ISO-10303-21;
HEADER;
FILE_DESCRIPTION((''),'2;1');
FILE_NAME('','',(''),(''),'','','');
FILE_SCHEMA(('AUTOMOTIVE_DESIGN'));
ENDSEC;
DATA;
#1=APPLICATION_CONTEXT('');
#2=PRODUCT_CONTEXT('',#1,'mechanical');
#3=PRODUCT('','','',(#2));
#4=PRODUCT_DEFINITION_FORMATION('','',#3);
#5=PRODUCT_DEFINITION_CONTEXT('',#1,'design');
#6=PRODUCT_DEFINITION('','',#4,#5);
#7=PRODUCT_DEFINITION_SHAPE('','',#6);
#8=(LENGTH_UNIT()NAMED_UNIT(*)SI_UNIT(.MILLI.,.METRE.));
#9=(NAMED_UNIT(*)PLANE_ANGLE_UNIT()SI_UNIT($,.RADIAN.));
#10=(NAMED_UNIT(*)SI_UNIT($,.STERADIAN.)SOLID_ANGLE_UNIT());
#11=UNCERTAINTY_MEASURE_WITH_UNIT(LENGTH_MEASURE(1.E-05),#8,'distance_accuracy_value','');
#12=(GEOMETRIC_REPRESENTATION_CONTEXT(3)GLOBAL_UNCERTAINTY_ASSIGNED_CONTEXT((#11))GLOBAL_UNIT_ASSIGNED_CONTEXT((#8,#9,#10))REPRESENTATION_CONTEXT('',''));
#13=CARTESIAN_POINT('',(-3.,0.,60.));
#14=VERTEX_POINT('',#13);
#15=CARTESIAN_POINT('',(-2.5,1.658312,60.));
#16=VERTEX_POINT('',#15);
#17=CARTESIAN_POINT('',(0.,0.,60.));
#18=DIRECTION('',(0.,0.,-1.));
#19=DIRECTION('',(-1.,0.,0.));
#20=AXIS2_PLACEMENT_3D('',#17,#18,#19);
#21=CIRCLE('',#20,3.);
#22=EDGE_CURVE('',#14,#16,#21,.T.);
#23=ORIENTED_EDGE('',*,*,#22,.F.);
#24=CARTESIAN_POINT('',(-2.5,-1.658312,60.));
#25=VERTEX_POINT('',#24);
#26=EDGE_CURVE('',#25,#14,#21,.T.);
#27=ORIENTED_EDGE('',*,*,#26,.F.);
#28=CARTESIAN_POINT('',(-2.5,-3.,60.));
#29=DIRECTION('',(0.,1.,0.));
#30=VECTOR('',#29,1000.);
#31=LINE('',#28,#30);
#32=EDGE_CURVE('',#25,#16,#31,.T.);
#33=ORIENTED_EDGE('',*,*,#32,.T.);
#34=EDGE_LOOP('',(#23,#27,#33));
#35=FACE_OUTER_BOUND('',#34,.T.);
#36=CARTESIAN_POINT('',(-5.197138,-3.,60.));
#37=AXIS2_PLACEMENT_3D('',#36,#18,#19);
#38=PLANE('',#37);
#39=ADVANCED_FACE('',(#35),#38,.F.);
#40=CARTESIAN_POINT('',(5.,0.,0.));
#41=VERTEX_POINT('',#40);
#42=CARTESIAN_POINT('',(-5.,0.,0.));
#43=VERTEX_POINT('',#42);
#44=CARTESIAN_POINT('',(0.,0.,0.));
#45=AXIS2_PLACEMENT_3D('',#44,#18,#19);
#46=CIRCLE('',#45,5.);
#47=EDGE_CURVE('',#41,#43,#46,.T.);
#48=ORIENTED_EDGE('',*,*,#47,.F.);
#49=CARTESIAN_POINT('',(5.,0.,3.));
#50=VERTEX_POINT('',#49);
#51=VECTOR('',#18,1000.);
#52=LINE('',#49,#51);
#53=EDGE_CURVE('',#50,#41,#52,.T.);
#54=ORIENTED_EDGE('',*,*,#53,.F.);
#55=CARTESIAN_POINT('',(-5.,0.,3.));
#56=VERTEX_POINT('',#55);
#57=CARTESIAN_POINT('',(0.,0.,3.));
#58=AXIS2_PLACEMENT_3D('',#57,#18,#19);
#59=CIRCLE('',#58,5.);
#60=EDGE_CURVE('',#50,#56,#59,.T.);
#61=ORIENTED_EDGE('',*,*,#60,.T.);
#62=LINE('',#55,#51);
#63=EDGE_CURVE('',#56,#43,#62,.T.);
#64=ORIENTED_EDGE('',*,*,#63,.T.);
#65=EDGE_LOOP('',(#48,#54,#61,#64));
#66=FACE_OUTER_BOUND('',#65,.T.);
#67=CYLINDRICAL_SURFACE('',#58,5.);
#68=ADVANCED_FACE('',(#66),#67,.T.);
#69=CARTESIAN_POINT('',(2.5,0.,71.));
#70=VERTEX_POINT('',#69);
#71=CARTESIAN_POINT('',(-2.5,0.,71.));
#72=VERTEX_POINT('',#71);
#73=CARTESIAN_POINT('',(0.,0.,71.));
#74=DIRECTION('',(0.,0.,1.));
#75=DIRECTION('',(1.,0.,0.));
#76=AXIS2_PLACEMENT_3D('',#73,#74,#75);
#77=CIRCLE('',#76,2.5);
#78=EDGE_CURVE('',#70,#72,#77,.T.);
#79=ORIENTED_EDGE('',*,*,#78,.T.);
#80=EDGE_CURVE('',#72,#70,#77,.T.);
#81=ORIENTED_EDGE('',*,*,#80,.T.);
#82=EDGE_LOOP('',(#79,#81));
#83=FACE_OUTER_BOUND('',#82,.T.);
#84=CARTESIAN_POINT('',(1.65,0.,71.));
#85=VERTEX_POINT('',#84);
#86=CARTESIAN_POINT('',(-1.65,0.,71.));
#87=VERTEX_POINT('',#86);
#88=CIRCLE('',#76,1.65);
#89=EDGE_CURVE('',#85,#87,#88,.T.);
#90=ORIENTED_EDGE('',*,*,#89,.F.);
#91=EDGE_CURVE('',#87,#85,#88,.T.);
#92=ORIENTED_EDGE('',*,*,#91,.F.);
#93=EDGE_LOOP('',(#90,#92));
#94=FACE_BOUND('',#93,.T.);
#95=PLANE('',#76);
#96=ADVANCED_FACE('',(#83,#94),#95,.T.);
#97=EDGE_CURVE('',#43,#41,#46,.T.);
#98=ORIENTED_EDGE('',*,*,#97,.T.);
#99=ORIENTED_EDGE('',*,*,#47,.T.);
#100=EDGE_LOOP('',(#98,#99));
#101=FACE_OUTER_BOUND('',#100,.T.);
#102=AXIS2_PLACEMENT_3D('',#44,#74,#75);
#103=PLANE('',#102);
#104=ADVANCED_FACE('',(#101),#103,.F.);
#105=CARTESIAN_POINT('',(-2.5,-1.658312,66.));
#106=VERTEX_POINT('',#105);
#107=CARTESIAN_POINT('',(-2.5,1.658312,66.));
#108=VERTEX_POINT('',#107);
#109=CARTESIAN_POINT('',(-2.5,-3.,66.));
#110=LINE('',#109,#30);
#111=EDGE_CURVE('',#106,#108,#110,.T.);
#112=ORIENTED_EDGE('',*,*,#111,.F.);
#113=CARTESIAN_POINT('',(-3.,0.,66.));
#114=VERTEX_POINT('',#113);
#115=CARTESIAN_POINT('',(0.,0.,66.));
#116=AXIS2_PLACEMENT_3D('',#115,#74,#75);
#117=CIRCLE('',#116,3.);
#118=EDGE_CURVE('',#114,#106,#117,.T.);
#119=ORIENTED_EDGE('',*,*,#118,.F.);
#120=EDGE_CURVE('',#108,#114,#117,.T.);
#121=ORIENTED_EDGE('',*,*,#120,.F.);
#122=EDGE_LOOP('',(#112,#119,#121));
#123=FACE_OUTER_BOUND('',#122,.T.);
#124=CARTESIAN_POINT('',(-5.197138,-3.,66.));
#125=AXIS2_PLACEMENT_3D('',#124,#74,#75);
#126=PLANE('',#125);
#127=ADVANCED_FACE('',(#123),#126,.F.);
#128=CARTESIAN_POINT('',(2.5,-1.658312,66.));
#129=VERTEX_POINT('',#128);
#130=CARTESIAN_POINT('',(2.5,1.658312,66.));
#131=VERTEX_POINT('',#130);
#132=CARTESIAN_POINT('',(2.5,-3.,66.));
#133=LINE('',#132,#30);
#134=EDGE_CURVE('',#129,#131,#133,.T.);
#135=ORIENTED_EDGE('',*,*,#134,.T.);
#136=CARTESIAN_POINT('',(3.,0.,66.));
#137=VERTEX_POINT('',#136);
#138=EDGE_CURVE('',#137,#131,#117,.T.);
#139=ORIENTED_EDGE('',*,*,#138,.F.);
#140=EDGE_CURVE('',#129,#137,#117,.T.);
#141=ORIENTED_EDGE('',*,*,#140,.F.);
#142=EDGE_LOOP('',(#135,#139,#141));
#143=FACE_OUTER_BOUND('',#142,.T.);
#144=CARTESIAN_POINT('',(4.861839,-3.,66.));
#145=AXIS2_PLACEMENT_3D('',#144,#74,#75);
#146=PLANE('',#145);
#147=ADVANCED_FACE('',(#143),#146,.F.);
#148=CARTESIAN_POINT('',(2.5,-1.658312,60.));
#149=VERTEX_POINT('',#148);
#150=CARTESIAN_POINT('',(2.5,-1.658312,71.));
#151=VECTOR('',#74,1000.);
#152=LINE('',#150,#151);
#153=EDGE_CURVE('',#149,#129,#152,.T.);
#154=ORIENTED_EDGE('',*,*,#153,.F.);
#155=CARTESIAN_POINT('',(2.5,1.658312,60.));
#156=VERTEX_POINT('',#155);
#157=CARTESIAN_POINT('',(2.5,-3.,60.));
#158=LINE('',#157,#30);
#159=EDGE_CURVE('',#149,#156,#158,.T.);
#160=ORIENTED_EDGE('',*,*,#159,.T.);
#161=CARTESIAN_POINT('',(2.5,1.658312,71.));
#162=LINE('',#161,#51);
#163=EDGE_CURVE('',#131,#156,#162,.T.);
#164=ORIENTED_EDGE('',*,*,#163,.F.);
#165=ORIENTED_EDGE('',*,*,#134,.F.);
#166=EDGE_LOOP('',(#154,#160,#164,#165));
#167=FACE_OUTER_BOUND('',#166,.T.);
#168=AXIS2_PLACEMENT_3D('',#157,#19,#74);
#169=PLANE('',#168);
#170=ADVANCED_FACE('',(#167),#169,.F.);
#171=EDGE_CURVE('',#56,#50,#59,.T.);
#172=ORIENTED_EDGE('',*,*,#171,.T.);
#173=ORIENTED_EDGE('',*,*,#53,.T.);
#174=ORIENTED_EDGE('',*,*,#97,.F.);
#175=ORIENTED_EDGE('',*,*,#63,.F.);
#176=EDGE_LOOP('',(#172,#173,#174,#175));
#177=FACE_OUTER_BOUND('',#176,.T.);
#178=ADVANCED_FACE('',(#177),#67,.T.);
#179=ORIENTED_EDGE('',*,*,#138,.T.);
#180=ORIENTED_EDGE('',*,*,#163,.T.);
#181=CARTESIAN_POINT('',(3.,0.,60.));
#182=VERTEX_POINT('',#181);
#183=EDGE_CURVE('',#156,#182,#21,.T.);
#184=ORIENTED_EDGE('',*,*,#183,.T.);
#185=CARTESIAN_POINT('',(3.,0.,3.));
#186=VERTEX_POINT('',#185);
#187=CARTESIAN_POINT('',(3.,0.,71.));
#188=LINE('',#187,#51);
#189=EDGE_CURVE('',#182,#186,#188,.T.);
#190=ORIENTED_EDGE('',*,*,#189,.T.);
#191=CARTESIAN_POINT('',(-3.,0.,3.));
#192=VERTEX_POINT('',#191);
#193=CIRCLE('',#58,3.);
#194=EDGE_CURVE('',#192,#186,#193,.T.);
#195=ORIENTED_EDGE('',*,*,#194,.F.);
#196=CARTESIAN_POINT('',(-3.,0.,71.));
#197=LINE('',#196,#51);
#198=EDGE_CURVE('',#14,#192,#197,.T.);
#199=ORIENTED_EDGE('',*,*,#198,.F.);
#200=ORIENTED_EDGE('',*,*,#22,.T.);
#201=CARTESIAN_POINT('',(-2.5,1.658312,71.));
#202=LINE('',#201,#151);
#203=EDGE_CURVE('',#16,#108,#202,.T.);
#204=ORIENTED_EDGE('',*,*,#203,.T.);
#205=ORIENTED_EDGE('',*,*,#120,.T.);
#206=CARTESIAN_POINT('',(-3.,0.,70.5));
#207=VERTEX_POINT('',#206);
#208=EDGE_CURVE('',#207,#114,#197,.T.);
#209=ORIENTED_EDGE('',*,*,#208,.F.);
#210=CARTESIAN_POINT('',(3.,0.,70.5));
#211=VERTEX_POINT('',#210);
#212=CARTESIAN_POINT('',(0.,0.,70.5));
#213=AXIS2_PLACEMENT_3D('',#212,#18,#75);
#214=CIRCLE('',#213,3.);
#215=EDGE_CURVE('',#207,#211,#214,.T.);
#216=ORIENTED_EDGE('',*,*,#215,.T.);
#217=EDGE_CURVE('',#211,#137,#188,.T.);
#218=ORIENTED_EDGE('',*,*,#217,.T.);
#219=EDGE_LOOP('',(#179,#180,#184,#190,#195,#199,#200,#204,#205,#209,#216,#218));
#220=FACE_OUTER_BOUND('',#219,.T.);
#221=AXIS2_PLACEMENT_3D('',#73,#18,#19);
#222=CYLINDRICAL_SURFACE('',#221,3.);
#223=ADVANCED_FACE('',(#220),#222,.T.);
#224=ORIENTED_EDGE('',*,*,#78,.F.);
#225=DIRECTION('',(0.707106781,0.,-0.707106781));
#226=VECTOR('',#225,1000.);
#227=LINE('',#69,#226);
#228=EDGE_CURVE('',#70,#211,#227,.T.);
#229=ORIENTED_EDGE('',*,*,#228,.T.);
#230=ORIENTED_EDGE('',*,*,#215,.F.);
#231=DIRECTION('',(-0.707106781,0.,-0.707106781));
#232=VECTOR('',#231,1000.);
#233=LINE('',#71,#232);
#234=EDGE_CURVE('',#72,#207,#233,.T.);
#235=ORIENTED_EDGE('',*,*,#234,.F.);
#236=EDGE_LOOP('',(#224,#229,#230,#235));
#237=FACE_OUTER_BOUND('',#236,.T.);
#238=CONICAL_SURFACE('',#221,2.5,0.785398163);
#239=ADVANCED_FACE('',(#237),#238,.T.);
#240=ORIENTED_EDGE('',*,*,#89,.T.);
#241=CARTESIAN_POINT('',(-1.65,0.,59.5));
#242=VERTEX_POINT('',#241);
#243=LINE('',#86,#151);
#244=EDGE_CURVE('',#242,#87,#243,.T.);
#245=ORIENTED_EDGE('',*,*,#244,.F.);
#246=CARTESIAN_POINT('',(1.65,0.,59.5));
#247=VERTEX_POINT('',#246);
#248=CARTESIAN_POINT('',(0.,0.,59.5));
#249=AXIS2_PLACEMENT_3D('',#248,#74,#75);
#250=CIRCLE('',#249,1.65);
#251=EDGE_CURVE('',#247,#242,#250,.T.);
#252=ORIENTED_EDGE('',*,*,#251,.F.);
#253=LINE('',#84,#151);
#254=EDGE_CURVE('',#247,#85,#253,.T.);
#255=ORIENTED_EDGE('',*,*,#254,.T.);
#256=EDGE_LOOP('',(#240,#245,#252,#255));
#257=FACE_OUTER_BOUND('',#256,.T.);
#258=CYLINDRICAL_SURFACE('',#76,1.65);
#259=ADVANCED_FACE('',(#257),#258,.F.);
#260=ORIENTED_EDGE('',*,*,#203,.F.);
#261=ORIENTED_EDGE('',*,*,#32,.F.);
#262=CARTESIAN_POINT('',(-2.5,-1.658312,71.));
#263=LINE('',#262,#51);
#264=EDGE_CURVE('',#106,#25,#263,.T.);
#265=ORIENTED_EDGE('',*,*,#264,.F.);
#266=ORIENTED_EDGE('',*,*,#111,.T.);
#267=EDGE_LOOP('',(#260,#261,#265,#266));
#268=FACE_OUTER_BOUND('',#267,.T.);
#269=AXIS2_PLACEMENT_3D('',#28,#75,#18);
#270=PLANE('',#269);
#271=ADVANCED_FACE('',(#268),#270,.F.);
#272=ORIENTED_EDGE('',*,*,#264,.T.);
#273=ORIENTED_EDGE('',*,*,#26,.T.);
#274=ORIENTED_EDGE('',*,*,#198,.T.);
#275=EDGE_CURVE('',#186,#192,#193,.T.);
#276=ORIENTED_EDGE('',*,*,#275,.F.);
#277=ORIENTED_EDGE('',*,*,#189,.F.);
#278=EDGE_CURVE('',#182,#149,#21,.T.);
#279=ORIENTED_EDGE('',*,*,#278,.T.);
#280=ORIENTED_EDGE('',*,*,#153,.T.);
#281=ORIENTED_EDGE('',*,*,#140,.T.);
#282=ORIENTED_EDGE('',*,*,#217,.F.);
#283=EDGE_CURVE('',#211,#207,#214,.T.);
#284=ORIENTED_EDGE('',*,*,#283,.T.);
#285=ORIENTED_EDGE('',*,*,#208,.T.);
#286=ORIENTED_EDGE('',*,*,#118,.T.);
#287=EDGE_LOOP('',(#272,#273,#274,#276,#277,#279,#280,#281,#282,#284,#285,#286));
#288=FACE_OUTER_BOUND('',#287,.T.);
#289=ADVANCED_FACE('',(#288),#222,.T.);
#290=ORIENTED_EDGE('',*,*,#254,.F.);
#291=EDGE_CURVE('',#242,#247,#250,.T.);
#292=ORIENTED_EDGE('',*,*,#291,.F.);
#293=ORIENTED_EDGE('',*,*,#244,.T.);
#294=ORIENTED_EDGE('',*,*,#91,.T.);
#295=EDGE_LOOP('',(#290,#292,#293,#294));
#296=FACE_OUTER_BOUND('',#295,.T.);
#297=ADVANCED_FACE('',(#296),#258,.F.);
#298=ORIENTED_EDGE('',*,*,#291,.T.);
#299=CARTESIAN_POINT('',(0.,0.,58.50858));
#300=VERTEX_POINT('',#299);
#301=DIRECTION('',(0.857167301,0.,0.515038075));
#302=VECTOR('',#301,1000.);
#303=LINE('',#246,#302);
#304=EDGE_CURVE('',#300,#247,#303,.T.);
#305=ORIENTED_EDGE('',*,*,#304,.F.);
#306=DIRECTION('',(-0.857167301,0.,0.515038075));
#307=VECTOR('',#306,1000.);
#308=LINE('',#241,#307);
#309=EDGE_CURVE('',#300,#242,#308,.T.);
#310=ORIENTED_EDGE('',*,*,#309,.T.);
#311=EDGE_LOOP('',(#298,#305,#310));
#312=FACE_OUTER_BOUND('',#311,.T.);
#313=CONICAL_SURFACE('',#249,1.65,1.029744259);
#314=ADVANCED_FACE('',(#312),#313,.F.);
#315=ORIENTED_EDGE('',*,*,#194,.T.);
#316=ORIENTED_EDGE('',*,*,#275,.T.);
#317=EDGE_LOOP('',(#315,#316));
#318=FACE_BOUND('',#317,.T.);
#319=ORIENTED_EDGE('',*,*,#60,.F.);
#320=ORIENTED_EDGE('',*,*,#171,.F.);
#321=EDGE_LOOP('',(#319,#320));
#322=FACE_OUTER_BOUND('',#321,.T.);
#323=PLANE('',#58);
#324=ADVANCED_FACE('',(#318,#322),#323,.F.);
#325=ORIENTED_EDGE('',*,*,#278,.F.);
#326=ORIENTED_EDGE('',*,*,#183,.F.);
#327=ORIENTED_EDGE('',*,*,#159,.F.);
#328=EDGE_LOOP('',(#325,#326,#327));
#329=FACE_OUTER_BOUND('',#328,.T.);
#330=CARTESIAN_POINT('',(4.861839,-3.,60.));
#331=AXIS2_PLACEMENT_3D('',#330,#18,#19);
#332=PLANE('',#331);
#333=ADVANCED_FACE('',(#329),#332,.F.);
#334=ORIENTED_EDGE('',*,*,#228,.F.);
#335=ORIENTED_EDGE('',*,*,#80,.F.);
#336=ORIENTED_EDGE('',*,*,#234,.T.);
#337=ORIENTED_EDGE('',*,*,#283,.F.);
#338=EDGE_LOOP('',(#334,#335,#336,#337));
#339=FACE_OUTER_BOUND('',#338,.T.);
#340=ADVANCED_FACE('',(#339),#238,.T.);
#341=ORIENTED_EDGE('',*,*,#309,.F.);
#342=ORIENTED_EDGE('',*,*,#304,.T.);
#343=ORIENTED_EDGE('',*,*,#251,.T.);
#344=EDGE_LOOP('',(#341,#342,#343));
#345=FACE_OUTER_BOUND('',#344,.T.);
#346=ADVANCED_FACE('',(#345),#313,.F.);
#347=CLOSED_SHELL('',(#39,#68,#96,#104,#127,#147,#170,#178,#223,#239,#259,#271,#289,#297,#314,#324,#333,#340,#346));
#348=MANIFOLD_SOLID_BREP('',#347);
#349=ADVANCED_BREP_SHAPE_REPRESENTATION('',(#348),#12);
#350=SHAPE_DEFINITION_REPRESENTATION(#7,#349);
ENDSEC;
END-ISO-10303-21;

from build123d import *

# Parameters (mm, degrees)
SKETCH_1_R             = 3
EXTRUDE_1_DEPTH        = 71
HOLE_WIZARD_M4_2_D     = 3.3
HOLE_WIZARD_M4_2_DEPTH = 11.5
HOLE_WIZARD_M4_2_TIP   = 0.991420021
CHAMFER_1_SIZE         = 0.5
EXTRUDE1_DEPTH         = 72.126647608
EXTRUDE1_DEPTH_BACK    = 72.126647608
SKETCH1_W              = 2.697137816
SKETCH1_H              = 6
SKETCH1_W_2            = 2.361838602
SKETCH4_R              = 5
SKETCH4_R_2            = 3
EXTRUDE2_DEPTH         = 3


with BuildPart() as part:
    # 草图1 → 凸台-拉伸1 (new body)
    with BuildSketch(Plane.XY):
        Circle(SKETCH_1_R)
    extrude(amount=EXTRUDE_1_DEPTH)

    # M4 螺纹孔2
    with Locations(Plane.XY.offset(71)):
        with Locations((0, 0)):
            Hole(HOLE_WIZARD_M4_2_D / 2, depth=HOLE_WIZARD_M4_2_DEPTH)
            with Locations((0, 0, -(HOLE_WIZARD_M4_2_DEPTH + HOLE_WIZARD_M4_2_TIP / 2))):  # 118° drill point
                Cone(0, HOLE_WIZARD_M4_2_D / 2, HOLE_WIZARD_M4_2_TIP, mode=Mode.SUBTRACT)

    # 倒角1
    chamfer_1_edges = [part.edges().sort_by_distance(p)[0] for p in [
        (-3, 0, 71),
    ]]
    chamfer(chamfer_1_edges, length=CHAMFER_1_SIZE)

    # Sketch1 → Extrude1 (cut, two sides: drawn at the far end of the back side and taken through both)
    with BuildSketch(Plane(origin=(0, 0, 0), x_dir=(1, 0, 0), z_dir=(0, 1, 0)).offset(-EXTRUDE1_DEPTH_BACK)):
        with Locations((-3.848568908, -63)):
            Rectangle(SKETCH1_W, SKETCH1_H)
        with Locations((3.680919301, -63)):
            Rectangle(SKETCH1_W_2, SKETCH1_H)
    extrude(amount=EXTRUDE1_DEPTH + EXTRUDE1_DEPTH_BACK, mode=Mode.SUBTRACT)

    # Sketch4 → Extrude2 (add)
    with BuildSketch(Plane(origin=(0, 0, 0), x_dir=(-1, 0, 0), z_dir=(0, 0, -1))):
        Circle(SKETCH4_R)
        Circle(SKETCH4_R_2, mode=Mode.SUBTRACT)
    extrude(amount=-EXTRUDE2_DEPTH)


solid = part.part
